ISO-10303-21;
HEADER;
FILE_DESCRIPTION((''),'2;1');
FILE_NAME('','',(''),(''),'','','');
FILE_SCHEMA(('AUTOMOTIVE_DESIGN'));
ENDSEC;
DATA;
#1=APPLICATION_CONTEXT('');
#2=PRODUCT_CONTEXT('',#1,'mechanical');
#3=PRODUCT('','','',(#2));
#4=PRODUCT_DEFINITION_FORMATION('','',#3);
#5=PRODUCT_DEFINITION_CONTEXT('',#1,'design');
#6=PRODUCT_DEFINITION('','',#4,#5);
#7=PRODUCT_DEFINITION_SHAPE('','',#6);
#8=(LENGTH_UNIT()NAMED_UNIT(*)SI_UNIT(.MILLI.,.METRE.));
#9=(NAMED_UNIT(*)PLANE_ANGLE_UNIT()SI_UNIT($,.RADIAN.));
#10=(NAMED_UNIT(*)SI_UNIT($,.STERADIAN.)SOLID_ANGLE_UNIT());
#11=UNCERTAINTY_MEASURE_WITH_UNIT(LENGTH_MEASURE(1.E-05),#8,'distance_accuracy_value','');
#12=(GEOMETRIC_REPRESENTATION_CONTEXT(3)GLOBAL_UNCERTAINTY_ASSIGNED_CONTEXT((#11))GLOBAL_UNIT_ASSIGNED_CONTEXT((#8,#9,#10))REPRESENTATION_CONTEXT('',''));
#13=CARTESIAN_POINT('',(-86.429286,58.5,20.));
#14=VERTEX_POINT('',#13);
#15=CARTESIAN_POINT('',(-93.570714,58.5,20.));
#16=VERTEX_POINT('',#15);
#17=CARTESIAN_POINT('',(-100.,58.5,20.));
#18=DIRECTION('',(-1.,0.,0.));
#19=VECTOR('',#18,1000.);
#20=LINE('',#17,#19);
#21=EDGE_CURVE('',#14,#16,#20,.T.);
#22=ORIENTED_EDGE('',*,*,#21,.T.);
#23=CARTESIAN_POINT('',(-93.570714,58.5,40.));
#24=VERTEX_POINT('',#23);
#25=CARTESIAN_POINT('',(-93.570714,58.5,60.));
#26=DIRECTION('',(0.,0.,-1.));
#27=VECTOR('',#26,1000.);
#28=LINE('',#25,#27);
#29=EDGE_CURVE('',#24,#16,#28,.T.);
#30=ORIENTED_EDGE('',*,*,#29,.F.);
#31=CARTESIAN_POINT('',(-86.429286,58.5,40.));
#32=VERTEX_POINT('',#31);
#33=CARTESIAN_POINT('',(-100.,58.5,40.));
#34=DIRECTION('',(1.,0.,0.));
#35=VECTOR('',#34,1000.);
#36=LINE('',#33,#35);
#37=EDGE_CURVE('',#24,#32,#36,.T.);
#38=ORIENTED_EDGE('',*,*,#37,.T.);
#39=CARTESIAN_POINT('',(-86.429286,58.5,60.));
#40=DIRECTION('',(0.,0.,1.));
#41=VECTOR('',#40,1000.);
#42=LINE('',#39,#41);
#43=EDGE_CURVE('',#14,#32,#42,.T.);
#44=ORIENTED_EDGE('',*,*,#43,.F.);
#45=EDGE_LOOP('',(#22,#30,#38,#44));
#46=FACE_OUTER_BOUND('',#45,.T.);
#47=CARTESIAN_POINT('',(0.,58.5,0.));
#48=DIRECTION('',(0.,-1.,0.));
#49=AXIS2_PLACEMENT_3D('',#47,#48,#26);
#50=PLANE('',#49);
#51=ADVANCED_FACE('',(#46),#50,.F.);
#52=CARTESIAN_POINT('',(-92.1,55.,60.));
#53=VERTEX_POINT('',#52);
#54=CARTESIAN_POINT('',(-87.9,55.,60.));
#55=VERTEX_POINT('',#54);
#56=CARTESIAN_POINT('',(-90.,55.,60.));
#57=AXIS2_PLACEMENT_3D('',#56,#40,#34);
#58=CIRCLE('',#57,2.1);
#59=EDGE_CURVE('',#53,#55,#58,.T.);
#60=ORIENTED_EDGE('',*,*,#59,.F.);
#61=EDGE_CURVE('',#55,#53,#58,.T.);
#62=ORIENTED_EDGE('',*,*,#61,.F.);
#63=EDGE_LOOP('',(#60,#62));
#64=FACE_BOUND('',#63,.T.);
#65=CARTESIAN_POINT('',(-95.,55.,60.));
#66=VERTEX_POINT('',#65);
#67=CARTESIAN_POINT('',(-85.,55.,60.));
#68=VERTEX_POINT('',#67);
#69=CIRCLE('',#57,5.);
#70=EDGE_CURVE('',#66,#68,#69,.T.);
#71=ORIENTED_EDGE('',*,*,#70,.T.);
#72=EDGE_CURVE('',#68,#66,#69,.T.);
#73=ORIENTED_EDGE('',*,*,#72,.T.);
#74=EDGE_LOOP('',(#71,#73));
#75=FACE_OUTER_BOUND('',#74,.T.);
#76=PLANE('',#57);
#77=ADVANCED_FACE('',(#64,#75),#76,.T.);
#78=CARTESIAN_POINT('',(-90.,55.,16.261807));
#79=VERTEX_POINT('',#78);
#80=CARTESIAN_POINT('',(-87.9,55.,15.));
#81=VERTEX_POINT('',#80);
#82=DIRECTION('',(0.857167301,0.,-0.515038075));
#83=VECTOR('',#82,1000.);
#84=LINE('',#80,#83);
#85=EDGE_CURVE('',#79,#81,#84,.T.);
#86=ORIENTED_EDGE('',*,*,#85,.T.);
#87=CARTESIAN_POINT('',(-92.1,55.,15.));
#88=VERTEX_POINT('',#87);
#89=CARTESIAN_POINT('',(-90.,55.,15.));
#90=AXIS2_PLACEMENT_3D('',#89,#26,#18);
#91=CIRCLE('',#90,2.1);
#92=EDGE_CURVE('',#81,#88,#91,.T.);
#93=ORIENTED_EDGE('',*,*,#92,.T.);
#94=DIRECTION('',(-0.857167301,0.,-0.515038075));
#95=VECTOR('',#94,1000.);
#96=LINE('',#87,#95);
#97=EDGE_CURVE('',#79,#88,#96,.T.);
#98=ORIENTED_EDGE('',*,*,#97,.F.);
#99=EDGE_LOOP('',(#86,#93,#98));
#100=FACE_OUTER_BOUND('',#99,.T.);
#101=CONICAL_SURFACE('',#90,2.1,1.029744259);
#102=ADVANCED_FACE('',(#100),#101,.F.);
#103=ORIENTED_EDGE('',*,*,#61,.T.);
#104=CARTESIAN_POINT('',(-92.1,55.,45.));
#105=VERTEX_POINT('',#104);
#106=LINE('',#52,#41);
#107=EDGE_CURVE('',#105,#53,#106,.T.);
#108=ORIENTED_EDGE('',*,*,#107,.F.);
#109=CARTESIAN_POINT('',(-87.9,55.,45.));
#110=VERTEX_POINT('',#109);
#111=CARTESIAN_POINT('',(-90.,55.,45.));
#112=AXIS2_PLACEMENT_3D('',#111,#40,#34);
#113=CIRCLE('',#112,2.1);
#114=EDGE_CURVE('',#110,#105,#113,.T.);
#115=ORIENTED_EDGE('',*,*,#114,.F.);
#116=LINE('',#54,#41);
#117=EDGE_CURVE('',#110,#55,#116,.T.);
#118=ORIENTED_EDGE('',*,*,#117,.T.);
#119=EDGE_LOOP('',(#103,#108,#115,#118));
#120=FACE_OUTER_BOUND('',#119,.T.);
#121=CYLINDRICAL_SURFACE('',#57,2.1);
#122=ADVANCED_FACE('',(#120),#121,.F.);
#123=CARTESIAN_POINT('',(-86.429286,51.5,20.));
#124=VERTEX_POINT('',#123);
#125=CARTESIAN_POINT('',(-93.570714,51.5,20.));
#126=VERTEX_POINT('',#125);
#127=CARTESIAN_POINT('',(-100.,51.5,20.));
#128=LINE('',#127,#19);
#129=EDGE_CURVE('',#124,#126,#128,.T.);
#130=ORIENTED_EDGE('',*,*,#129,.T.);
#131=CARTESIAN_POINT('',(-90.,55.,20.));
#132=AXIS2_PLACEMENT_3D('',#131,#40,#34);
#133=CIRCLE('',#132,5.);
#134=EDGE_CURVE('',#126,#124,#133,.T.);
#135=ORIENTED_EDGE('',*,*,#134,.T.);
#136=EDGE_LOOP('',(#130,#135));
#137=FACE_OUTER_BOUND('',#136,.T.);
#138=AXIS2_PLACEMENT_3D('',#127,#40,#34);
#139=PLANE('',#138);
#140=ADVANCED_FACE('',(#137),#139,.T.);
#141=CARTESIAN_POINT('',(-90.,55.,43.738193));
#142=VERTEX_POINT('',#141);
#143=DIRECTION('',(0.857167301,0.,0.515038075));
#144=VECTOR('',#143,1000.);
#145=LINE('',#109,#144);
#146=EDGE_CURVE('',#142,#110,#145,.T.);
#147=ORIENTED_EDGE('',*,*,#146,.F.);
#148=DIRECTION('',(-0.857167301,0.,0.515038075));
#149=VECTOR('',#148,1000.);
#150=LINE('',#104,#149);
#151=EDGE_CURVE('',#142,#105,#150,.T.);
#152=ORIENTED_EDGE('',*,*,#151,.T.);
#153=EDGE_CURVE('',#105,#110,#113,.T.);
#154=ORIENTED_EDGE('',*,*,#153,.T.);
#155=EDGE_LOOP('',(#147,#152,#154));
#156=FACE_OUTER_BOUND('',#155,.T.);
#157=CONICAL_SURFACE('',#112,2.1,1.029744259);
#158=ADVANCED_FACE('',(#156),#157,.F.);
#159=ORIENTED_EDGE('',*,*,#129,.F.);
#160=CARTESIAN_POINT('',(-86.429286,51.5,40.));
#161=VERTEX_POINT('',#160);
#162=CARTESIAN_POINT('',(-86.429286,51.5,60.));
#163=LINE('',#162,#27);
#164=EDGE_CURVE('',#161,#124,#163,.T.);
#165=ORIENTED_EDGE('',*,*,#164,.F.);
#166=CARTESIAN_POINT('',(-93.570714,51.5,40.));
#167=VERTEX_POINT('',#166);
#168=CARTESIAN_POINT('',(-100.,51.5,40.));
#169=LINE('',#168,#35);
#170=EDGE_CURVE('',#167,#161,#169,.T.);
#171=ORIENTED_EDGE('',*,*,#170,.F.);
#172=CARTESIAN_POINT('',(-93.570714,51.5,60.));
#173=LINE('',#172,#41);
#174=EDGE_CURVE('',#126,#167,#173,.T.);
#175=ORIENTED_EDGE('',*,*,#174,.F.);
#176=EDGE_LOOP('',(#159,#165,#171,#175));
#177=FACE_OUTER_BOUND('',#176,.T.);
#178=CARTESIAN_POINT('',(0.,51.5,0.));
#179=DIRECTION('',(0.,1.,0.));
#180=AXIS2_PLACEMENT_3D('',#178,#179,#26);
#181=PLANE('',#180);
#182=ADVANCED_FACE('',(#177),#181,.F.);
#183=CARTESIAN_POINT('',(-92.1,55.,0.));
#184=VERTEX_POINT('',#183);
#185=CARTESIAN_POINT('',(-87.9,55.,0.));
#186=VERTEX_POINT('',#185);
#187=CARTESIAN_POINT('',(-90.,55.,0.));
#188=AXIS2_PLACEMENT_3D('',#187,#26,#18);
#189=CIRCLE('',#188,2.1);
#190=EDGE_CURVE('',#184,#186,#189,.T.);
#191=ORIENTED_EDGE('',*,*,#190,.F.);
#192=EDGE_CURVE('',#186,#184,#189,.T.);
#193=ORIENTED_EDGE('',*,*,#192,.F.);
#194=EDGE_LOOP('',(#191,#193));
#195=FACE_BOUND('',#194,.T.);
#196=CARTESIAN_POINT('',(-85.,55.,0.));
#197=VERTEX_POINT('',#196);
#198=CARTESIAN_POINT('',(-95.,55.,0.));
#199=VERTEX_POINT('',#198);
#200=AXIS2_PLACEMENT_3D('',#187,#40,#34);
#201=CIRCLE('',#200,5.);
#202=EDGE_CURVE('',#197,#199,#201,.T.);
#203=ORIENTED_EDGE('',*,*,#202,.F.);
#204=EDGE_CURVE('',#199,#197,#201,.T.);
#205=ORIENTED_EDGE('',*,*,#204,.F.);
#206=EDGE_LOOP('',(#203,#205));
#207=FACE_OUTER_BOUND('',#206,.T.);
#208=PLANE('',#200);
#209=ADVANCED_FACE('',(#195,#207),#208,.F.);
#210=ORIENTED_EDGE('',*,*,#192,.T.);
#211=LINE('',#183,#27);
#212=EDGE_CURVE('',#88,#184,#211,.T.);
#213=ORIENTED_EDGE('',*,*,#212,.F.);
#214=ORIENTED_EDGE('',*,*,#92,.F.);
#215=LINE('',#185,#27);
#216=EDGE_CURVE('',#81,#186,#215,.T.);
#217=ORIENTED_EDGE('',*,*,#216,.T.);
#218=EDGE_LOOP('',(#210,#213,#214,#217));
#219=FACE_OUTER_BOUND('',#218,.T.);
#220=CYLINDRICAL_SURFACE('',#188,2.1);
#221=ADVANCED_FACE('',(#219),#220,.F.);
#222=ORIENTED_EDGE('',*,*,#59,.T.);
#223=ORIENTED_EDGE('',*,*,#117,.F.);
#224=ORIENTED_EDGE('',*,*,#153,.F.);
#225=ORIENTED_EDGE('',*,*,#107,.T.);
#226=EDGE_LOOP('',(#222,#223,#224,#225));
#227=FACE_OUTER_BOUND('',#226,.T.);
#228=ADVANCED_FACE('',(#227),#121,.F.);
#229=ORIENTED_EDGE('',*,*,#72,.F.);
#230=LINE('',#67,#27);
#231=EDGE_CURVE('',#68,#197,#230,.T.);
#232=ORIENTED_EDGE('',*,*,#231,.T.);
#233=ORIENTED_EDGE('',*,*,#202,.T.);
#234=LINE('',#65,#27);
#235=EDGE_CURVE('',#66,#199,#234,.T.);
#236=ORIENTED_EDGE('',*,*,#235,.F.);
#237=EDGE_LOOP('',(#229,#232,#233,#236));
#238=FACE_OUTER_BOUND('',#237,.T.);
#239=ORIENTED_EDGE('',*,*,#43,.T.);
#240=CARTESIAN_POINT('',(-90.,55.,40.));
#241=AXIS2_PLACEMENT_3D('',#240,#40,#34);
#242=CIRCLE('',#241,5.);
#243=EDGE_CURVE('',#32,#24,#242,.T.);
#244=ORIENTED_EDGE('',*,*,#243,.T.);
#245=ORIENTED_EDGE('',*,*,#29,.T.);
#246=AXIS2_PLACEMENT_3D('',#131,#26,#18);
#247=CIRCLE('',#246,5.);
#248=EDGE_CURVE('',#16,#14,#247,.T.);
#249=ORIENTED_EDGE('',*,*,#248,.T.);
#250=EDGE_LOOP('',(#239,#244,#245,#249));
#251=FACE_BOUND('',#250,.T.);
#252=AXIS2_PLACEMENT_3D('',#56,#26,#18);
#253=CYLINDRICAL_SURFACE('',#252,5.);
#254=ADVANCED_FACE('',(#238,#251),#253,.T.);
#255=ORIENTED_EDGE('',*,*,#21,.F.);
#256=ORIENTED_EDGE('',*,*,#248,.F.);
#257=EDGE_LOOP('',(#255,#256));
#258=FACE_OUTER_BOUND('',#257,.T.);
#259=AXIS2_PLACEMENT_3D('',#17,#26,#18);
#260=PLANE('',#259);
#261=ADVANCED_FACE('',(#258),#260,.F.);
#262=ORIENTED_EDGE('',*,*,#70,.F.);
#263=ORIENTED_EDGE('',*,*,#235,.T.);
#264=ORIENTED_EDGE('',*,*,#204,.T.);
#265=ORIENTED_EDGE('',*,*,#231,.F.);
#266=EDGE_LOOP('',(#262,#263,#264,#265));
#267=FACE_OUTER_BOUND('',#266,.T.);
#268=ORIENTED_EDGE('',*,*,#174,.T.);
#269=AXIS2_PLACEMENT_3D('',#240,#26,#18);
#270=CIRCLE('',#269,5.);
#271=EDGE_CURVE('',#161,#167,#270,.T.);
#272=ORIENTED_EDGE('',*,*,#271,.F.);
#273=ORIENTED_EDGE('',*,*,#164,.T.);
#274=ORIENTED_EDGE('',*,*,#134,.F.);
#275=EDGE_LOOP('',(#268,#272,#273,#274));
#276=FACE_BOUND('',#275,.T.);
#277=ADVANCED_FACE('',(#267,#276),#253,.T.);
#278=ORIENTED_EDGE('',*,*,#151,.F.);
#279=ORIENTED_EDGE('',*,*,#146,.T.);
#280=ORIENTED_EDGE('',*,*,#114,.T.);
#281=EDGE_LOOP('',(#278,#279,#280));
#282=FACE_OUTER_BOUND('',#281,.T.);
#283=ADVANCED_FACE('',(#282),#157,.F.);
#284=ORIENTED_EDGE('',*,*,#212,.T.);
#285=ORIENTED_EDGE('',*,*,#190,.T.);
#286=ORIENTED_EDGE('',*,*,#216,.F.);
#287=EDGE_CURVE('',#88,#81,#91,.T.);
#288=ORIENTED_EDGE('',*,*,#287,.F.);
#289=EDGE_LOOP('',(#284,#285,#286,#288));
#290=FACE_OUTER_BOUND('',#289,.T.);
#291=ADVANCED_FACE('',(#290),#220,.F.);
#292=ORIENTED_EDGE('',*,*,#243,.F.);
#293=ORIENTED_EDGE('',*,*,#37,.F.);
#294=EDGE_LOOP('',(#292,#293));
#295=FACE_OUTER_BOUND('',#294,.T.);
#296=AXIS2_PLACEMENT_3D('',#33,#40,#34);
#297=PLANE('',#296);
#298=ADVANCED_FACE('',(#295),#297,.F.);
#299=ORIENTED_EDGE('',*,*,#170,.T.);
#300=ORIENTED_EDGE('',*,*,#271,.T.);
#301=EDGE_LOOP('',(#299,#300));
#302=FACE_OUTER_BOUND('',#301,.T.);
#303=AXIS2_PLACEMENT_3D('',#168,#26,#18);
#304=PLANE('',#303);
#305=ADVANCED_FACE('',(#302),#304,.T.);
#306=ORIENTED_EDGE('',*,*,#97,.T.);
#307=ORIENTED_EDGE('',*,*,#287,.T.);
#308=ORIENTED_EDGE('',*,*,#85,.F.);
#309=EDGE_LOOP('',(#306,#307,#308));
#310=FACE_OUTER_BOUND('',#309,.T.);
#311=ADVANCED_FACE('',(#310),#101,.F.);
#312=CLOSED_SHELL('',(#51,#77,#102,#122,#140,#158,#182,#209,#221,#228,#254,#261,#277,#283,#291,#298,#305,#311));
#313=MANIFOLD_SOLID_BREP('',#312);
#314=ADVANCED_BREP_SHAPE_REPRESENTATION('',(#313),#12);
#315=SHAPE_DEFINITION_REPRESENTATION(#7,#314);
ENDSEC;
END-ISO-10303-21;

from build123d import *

# Parameters (mm, degrees)
SKETCH1_R                       = 5
BOSS_EXTRUDE1_DEPTH             = 60
SKETCH2_W                       = 20
SKETCH2_H                       = 20
CUT_EXTRUDE1_DEPTH              = 1.5
M5_TAPPED_HOLE1_D               = 4.2
M5_TAPPED_HOLE1_DEPTH           = 15
M5_TAPPED_HOLE1_TIP             = 1.2618073
M5_TAPPED_HOLE1_ON_FACE_2_D     = 4.2
M5_TAPPED_HOLE1_ON_FACE_2_DEPTH = 15
M5_TAPPED_HOLE1_ON_FACE_2_TIP   = 1.2618073


with BuildPart() as part:
    # Sketch1 → Boss-Extrude1 (new body)
    with BuildSketch(Plane.XY):
        with Locations((-90, 55)):
            Circle(SKETCH1_R)
    extrude(amount=BOSS_EXTRUDE1_DEPTH)

    # Sketch2 → Cut-Extrude1 (cut)
    with BuildSketch(Plane(origin=(0, 60, 0), x_dir=(1, 0, 0), z_dir=(0, 1, 0))):
        with Locations((-90, -30)):
            Rectangle(SKETCH2_W, SKETCH2_H)
    cut_extrude1 = extrude(amount=-CUT_EXTRUDE1_DEPTH, mode=Mode.SUBTRACT)

    # Mirror1: Cut-Extrude1 across plane
    add(cut_extrude1.mirror(Plane.ZX.offset(55)), mode=Mode.SUBTRACT)

    # M5 Tapped Hole1
    with Locations(Plane(origin=(-90, 55, 0), x_dir=(-1, 0, 0), z_dir=(0, 0, -1))):
        with Locations((0, 0)):
            Hole(M5_TAPPED_HOLE1_D / 2, depth=M5_TAPPED_HOLE1_DEPTH)
            with Locations((0, 0, -(M5_TAPPED_HOLE1_DEPTH + M5_TAPPED_HOLE1_TIP / 2))):  # 118° drill point
                Cone(0, M5_TAPPED_HOLE1_D / 2, M5_TAPPED_HOLE1_TIP, mode=Mode.SUBTRACT)

    # M5 Tapped Hole1 on face 2
    with Locations(Plane(origin=(-90, 55, 60), x_dir=(1, 0, 0), z_dir=(0, 0, 1))):
        with Locations((0, 0)):
            Hole(M5_TAPPED_HOLE1_ON_FACE_2_D / 2, depth=M5_TAPPED_HOLE1_ON_FACE_2_DEPTH)
            with Locations((0, 0, -(M5_TAPPED_HOLE1_ON_FACE_2_DEPTH + M5_TAPPED_HOLE1_ON_FACE_2_TIP / 2))):  # 118° drill point
                Cone(0, M5_TAPPED_HOLE1_ON_FACE_2_D / 2, M5_TAPPED_HOLE1_ON_FACE_2_TIP, mode=Mode.SUBTRACT)


solid = part.part
